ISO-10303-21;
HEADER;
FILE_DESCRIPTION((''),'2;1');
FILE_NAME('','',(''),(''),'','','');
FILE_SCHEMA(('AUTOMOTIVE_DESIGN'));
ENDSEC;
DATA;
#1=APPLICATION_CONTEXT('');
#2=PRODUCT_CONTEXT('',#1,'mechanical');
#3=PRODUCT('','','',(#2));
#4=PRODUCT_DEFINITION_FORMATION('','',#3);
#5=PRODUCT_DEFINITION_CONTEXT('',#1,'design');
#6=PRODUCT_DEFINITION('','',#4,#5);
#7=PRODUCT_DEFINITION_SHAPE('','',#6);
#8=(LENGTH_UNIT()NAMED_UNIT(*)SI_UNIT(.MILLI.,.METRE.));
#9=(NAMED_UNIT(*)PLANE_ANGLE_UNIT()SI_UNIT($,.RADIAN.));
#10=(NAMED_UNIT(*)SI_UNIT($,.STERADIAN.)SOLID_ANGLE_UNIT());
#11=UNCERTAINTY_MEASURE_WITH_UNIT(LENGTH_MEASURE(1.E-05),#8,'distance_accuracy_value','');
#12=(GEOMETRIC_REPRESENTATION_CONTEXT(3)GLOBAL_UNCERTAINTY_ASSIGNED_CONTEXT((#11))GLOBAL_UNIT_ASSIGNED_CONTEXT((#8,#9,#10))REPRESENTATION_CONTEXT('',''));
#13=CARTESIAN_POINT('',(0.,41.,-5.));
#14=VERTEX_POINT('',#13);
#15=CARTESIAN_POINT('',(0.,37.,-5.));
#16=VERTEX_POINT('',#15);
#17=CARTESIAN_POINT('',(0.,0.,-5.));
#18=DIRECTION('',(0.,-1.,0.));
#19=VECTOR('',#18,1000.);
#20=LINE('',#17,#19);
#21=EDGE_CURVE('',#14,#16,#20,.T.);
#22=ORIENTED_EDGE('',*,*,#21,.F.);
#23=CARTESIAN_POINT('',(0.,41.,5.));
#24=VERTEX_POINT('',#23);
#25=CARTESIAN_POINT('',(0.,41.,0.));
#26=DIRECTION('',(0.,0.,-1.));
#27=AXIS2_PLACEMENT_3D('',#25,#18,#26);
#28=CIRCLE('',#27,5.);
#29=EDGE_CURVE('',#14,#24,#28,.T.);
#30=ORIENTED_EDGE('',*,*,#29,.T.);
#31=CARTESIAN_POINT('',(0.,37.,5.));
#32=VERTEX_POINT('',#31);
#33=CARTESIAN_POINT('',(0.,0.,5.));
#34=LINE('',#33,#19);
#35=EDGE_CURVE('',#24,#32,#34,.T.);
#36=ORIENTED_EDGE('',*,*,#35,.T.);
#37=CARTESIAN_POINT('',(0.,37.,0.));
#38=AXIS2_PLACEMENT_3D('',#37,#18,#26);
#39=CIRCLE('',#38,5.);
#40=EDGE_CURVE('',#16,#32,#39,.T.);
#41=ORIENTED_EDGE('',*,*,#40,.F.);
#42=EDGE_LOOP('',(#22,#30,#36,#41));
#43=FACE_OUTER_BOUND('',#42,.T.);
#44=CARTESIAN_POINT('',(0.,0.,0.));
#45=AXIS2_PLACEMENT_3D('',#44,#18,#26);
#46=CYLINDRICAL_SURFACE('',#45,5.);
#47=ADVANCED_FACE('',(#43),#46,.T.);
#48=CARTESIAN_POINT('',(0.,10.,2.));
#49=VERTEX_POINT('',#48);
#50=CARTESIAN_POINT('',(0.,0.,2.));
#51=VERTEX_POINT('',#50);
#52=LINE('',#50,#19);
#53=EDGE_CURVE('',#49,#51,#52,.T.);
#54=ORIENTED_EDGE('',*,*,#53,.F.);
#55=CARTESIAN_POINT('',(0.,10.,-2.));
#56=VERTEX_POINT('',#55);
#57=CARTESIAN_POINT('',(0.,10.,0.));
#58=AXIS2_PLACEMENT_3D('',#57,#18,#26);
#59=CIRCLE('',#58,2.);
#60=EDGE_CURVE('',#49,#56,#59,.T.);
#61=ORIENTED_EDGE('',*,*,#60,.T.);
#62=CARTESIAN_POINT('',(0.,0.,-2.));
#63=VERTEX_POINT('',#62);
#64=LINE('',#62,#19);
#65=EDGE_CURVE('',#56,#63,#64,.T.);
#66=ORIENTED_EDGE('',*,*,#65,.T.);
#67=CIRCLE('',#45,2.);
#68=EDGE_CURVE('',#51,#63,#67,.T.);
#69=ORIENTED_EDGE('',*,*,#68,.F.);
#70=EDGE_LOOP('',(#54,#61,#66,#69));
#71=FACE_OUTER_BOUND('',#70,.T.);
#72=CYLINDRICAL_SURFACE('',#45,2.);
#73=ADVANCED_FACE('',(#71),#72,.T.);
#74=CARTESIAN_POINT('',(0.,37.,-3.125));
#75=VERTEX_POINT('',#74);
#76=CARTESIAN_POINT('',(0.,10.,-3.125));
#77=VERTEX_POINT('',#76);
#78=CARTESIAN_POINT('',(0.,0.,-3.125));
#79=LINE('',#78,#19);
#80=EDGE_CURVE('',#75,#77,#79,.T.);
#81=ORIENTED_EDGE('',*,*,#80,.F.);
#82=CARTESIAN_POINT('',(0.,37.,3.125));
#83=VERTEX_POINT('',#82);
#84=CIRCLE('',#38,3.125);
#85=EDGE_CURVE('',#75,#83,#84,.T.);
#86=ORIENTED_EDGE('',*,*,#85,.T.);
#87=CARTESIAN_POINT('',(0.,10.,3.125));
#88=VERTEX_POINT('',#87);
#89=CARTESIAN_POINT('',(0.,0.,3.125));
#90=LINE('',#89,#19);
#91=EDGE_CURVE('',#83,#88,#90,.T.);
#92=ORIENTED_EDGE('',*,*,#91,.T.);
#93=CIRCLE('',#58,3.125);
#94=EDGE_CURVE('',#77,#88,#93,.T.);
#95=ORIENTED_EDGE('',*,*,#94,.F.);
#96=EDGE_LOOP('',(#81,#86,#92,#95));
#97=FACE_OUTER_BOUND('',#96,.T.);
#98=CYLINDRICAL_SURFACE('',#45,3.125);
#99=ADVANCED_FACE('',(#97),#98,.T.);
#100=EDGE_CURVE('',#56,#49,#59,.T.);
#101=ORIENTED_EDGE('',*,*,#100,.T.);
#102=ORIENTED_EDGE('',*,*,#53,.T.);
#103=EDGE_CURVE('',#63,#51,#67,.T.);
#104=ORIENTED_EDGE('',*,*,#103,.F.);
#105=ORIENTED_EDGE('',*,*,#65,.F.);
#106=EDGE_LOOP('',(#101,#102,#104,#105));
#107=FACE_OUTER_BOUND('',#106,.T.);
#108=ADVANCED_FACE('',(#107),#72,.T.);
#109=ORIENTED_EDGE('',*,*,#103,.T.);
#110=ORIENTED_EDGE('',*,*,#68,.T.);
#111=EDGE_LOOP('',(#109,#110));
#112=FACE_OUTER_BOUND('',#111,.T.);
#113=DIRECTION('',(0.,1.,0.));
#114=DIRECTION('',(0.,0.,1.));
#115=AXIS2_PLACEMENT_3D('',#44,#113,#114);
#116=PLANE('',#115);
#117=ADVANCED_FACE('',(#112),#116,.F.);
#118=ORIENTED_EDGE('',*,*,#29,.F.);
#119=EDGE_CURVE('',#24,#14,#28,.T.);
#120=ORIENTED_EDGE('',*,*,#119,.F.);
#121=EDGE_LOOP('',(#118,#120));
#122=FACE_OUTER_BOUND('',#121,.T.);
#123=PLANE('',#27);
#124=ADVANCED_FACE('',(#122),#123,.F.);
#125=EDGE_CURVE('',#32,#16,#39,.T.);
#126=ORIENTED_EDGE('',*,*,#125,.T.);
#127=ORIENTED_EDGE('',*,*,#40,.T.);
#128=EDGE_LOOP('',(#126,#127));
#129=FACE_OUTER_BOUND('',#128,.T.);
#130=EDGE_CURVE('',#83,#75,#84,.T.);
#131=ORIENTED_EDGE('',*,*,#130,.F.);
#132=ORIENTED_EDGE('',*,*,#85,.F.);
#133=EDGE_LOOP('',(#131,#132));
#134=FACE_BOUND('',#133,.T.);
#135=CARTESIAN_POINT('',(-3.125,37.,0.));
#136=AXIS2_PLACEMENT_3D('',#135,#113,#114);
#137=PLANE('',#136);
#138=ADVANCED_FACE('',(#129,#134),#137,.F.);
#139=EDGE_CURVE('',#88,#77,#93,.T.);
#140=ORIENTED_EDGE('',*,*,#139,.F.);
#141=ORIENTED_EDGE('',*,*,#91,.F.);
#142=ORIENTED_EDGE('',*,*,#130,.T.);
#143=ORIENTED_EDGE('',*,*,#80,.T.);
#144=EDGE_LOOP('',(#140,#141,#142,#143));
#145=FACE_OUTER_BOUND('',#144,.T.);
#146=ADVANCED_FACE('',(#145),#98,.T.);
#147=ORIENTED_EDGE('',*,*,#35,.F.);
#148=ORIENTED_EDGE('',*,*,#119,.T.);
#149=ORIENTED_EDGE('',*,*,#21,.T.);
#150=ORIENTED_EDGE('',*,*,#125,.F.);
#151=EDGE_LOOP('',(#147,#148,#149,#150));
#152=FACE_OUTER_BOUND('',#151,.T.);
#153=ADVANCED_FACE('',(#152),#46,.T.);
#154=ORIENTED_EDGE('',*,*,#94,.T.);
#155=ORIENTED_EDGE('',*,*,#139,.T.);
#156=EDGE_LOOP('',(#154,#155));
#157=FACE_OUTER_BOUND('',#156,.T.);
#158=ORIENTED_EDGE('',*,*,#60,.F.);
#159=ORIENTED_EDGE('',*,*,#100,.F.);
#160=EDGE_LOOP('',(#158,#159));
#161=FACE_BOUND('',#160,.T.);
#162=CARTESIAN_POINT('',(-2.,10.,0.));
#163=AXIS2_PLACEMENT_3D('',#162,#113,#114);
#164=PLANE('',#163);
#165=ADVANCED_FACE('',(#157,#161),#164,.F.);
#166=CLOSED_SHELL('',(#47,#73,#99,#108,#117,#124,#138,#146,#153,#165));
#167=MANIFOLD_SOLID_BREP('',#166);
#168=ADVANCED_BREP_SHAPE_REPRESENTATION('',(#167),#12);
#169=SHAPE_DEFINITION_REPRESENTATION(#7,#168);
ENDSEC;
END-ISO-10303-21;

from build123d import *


with BuildPart() as part:
    # Screw Profile Sketch → Screw Body Revolve (revolve)
    with BuildSketch(Plane.XY, mode=Mode.PRIVATE) as screw_body_revolve_sk:
        Polygon((0, 0), (-2, 0), (-2, 10), (-3.125, 10), (-3.125, 37), (-5, 37), (-5, 41), (0, 41), align=None)
    revolve(screw_body_revolve_sk.sketch.rotate(Axis((0, 0, 0), (0, 1, 0)), 270), axis=Axis((0, 0, 0), (0, 1, 0)))


solid = part.part
